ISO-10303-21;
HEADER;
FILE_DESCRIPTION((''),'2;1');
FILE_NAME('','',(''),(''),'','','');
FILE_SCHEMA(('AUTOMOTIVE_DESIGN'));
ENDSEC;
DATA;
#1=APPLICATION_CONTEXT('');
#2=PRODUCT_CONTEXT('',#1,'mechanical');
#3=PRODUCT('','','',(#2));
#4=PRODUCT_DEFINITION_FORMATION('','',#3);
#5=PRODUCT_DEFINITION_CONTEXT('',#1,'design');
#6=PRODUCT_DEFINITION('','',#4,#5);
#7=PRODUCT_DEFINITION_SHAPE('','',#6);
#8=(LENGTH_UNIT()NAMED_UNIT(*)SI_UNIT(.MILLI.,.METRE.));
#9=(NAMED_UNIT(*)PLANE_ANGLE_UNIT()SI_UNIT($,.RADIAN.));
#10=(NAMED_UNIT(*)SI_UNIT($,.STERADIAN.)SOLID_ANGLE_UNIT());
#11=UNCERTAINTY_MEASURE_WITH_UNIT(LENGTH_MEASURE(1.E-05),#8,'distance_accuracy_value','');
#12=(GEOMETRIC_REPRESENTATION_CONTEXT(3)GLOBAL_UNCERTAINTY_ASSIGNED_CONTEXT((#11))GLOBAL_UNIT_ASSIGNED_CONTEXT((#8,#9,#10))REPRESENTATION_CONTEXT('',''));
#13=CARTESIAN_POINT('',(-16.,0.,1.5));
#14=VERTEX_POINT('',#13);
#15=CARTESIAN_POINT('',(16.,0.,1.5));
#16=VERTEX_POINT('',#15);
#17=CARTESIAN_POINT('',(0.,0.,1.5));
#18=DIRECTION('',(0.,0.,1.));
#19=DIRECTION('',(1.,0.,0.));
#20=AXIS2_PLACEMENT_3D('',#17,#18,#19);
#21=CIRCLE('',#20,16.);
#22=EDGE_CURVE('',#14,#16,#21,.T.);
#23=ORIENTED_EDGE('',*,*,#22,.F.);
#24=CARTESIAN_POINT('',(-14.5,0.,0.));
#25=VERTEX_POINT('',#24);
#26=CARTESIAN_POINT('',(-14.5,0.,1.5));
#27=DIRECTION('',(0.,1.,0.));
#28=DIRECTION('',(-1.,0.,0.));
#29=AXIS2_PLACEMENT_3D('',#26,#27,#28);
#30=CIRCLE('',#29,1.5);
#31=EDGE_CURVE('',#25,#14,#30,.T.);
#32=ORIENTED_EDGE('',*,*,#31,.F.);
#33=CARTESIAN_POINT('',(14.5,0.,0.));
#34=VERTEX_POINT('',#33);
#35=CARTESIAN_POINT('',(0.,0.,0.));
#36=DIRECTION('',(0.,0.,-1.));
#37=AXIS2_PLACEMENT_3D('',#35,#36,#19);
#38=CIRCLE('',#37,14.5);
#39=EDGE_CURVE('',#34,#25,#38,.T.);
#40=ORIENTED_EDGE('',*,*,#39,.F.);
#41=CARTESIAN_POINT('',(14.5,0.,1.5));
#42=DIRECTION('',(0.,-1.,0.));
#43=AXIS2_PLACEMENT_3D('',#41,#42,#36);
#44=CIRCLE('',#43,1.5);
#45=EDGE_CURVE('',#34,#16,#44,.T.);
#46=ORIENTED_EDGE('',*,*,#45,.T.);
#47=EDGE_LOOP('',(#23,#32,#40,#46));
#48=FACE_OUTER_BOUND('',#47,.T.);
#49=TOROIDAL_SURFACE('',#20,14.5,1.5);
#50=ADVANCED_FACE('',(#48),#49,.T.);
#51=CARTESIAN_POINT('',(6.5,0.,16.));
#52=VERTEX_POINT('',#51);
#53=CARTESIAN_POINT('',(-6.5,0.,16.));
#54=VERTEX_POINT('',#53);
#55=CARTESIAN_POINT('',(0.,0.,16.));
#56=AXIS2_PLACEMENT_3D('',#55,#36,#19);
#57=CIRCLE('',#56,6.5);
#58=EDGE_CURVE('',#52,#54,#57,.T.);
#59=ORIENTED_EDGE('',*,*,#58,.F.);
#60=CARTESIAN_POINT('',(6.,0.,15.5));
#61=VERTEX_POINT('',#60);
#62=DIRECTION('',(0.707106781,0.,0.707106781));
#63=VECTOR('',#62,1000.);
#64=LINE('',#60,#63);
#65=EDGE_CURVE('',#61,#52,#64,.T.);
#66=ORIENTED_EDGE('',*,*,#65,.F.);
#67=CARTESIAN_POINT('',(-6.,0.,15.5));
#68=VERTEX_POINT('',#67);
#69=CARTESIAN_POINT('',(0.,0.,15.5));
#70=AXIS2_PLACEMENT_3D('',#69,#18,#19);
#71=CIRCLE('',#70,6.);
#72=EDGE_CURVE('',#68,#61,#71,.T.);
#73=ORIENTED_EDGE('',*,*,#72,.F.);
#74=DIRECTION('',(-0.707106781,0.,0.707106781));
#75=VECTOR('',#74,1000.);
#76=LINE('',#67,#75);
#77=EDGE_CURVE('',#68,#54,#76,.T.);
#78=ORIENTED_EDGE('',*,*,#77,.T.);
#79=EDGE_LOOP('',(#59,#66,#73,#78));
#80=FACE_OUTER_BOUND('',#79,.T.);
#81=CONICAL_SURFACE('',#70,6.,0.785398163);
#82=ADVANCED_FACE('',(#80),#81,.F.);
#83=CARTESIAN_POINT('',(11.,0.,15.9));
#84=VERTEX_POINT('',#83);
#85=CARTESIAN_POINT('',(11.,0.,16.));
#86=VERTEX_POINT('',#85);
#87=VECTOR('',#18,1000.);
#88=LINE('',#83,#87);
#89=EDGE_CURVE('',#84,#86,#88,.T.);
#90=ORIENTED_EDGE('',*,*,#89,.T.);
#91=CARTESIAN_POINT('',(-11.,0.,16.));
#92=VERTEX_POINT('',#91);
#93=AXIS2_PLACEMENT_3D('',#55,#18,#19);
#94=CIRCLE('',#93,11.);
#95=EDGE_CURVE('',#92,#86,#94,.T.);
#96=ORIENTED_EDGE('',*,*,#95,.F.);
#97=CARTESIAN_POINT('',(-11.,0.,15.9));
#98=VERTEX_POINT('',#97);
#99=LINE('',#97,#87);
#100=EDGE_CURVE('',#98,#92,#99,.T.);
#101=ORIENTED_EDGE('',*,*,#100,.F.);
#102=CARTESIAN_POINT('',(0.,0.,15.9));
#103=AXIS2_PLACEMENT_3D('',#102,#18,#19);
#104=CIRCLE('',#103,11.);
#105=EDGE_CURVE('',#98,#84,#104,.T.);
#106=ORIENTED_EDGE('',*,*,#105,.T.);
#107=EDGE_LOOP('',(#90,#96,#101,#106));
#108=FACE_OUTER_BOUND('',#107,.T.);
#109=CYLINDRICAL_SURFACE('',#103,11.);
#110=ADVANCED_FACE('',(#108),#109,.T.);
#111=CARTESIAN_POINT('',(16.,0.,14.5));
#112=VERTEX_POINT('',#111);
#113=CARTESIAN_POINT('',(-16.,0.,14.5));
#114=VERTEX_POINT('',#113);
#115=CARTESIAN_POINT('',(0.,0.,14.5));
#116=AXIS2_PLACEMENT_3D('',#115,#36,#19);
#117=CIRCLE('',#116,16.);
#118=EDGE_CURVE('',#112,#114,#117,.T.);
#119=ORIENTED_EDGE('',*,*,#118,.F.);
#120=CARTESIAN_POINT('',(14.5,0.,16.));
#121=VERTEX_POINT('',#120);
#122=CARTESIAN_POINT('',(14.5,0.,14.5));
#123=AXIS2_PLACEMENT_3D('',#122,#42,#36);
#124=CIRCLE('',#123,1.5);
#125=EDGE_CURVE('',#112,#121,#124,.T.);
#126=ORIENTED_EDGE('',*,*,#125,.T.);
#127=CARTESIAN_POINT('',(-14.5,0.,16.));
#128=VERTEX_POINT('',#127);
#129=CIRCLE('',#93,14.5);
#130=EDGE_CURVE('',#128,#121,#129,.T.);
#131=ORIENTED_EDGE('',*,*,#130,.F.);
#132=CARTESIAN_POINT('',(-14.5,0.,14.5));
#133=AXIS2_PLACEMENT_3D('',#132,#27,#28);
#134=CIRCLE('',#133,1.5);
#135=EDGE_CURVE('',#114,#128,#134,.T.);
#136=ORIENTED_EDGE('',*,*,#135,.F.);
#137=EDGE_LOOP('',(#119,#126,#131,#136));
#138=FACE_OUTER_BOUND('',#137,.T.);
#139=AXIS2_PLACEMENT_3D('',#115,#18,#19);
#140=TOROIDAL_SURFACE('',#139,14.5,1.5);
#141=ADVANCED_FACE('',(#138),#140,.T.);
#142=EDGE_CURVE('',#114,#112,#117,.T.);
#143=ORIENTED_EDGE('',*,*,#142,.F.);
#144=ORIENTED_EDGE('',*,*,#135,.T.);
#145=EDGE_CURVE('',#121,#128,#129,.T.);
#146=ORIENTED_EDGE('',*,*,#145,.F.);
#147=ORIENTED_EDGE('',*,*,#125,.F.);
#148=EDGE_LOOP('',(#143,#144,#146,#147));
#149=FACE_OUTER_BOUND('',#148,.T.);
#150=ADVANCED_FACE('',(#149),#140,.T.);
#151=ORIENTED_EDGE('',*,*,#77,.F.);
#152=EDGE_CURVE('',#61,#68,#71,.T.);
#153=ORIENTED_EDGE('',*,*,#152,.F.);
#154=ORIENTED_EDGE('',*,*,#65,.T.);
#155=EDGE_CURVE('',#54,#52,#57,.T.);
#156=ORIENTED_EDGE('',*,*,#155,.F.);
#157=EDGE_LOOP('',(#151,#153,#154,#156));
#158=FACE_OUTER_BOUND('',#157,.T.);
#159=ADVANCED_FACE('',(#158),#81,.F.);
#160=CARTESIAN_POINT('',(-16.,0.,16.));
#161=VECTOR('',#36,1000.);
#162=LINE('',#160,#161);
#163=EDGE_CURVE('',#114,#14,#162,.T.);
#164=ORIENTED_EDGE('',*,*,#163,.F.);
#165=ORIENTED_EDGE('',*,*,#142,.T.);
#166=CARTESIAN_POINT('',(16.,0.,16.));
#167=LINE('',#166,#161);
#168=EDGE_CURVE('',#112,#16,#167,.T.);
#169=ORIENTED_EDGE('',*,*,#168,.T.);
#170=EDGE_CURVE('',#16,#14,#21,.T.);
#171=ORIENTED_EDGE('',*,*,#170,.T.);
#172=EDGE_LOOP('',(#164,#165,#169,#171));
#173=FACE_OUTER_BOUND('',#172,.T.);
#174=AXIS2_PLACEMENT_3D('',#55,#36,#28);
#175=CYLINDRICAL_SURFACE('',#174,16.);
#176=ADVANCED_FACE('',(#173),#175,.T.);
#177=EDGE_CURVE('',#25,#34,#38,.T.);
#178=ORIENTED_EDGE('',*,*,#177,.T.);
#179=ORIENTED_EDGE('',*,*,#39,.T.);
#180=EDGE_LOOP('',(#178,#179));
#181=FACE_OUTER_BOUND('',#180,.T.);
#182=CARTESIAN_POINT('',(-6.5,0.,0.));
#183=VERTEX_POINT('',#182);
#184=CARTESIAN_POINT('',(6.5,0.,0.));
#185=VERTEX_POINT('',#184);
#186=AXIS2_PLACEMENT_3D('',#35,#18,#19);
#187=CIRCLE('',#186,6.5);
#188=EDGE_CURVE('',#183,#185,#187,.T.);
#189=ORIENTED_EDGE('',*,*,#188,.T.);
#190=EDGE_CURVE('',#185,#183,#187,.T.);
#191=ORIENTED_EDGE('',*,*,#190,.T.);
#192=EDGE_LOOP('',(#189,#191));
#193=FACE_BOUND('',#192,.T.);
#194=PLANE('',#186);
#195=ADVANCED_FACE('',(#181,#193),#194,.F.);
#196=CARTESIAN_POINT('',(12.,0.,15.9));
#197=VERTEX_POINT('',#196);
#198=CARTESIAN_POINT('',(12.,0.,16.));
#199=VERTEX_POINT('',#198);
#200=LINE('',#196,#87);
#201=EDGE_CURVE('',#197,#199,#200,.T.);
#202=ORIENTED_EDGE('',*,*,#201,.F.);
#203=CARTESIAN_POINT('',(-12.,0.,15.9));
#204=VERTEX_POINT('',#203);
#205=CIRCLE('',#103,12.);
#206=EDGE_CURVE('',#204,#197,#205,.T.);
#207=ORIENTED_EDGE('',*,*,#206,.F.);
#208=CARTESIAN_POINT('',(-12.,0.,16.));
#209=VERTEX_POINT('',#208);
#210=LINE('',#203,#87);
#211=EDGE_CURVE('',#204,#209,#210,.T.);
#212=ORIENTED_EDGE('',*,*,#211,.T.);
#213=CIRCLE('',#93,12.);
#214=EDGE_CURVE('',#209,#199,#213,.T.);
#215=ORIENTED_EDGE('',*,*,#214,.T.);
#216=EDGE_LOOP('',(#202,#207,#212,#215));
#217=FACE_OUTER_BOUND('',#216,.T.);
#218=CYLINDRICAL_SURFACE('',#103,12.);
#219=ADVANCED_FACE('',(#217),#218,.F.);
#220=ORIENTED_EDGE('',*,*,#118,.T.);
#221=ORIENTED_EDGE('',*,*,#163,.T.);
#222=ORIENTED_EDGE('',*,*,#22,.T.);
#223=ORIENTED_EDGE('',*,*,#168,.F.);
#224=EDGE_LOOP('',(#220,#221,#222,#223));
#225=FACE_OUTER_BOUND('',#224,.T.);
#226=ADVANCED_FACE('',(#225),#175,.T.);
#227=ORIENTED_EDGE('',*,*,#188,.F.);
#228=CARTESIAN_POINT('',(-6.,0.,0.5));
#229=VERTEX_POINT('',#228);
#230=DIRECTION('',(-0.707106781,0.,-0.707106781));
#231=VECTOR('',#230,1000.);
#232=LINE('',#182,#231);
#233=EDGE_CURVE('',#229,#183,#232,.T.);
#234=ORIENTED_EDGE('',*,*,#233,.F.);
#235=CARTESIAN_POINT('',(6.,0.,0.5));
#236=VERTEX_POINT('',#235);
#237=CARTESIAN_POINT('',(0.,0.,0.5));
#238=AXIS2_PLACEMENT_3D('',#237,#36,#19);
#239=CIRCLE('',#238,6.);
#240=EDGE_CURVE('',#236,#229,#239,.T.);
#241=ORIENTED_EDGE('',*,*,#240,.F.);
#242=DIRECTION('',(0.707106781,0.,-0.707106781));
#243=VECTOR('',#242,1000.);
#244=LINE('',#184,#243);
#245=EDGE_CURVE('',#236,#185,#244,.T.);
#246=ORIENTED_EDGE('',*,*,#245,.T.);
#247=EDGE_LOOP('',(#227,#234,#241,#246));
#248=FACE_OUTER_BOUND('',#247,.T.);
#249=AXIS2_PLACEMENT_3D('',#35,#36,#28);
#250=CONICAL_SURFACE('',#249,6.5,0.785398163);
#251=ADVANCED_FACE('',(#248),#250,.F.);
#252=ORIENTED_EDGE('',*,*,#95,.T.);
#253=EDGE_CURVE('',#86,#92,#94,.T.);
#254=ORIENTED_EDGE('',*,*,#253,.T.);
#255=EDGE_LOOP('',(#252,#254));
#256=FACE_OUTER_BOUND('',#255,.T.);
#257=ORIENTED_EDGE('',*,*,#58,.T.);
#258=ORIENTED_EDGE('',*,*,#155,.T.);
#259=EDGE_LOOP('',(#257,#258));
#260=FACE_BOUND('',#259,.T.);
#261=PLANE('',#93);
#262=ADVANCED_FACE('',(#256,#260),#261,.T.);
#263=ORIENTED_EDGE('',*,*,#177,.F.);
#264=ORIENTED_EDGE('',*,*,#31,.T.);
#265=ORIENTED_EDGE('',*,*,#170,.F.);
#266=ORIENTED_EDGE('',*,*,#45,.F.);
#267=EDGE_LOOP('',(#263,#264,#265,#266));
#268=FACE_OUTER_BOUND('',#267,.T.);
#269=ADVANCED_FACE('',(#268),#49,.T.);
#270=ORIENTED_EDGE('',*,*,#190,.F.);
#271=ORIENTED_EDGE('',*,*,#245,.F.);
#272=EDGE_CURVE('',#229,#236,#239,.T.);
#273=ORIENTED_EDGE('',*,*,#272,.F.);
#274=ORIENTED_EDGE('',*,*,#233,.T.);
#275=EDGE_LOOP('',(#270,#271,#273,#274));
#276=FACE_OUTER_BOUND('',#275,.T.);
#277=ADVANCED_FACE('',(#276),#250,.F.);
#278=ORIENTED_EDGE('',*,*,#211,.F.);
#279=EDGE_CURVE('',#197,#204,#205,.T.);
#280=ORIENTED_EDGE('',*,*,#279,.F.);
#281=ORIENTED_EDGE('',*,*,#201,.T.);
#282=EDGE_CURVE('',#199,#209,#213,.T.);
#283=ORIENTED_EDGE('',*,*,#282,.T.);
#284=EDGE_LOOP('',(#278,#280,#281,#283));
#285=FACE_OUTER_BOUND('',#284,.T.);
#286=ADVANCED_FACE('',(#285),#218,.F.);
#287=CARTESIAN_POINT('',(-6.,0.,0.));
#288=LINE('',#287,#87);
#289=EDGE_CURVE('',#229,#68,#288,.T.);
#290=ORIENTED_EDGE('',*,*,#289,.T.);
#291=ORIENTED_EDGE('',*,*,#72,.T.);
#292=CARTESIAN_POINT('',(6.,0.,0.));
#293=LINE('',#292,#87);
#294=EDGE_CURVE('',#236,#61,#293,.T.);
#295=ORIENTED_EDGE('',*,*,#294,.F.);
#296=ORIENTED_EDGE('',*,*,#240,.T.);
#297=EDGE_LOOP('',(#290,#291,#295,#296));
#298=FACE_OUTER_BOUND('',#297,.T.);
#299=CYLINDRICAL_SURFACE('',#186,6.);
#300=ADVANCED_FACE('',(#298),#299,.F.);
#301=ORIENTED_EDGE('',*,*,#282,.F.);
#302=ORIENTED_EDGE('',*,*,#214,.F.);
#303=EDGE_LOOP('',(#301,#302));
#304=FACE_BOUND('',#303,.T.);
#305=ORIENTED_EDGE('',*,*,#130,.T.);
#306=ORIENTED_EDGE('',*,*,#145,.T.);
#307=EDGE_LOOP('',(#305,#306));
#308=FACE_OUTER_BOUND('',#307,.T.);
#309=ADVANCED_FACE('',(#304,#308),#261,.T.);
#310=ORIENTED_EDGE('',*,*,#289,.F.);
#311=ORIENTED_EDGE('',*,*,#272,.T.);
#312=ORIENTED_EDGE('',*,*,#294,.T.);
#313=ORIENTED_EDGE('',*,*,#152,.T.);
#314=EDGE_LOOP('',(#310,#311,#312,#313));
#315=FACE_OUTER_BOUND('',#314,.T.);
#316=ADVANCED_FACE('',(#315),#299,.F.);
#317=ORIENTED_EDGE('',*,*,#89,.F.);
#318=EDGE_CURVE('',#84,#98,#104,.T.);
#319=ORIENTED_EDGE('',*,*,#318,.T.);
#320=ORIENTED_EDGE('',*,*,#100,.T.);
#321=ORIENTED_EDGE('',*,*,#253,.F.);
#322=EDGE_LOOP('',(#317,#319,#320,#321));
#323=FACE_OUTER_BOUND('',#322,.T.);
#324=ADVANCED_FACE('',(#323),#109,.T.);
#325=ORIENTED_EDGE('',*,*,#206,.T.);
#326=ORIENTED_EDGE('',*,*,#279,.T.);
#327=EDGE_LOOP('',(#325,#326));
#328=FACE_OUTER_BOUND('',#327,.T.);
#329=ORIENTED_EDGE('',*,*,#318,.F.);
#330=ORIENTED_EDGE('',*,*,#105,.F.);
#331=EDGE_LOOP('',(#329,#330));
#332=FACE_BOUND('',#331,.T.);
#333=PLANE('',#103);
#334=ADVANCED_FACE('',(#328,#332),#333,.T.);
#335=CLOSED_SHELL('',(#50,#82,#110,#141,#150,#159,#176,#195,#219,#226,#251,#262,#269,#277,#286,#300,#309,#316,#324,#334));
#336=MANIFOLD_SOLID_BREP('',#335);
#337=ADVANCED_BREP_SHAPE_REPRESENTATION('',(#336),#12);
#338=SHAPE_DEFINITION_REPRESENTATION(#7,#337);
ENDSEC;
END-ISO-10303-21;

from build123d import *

# Parameters (mm, degrees)
SKETCH1_R           = 16
BOSS_EXTRUDE1_DEPTH = 16
SKETCH2_R           = 6
CUT_EXTRUDE1_DEPTH  = 16
SKETCH3_R           = 12
SKETCH3_R_2         = 11
CUT_EXTRUDE2_DEPTH  = 0.1
FILLET1_R           = 1.5
CHAMFER1_SIZE       = 0.5


with BuildPart() as part:
    # Sketch1 → Boss-Extrude1 (new body)
    with BuildSketch(Plane.XY):
        Circle(SKETCH1_R)
    extrude(amount=BOSS_EXTRUDE1_DEPTH)

    # Sketch2 → Cut-Extrude1 (cut)
    with BuildSketch(Plane.XY.offset(16)):
        Circle(SKETCH2_R)
    extrude(amount=-CUT_EXTRUDE1_DEPTH, mode=Mode.SUBTRACT)

    # Sketch3 → Cut-Extrude2 (cut)
    with BuildSketch(Plane.XY.offset(16)):
        Circle(SKETCH3_R)
        Circle(SKETCH3_R_2, mode=Mode.SUBTRACT)
    extrude(amount=-CUT_EXTRUDE2_DEPTH, mode=Mode.SUBTRACT)

    # Fillet1
    fillet1_edges = [part.edges().sort_by_distance(p)[0] for p in [
        (-16, 0, 0),
        (-16, 0, 16),
    ]]
    fillet(fillet1_edges, radius=FILLET1_R)

    # Chamfer1
    chamfer1_edges = [part.edges().sort_by_distance(p)[0] for p in [
        (-6, 0, 0),
        (-6, 0, 16),
    ]]
    chamfer(chamfer1_edges, length=CHAMFER1_SIZE)


solid = part.part
